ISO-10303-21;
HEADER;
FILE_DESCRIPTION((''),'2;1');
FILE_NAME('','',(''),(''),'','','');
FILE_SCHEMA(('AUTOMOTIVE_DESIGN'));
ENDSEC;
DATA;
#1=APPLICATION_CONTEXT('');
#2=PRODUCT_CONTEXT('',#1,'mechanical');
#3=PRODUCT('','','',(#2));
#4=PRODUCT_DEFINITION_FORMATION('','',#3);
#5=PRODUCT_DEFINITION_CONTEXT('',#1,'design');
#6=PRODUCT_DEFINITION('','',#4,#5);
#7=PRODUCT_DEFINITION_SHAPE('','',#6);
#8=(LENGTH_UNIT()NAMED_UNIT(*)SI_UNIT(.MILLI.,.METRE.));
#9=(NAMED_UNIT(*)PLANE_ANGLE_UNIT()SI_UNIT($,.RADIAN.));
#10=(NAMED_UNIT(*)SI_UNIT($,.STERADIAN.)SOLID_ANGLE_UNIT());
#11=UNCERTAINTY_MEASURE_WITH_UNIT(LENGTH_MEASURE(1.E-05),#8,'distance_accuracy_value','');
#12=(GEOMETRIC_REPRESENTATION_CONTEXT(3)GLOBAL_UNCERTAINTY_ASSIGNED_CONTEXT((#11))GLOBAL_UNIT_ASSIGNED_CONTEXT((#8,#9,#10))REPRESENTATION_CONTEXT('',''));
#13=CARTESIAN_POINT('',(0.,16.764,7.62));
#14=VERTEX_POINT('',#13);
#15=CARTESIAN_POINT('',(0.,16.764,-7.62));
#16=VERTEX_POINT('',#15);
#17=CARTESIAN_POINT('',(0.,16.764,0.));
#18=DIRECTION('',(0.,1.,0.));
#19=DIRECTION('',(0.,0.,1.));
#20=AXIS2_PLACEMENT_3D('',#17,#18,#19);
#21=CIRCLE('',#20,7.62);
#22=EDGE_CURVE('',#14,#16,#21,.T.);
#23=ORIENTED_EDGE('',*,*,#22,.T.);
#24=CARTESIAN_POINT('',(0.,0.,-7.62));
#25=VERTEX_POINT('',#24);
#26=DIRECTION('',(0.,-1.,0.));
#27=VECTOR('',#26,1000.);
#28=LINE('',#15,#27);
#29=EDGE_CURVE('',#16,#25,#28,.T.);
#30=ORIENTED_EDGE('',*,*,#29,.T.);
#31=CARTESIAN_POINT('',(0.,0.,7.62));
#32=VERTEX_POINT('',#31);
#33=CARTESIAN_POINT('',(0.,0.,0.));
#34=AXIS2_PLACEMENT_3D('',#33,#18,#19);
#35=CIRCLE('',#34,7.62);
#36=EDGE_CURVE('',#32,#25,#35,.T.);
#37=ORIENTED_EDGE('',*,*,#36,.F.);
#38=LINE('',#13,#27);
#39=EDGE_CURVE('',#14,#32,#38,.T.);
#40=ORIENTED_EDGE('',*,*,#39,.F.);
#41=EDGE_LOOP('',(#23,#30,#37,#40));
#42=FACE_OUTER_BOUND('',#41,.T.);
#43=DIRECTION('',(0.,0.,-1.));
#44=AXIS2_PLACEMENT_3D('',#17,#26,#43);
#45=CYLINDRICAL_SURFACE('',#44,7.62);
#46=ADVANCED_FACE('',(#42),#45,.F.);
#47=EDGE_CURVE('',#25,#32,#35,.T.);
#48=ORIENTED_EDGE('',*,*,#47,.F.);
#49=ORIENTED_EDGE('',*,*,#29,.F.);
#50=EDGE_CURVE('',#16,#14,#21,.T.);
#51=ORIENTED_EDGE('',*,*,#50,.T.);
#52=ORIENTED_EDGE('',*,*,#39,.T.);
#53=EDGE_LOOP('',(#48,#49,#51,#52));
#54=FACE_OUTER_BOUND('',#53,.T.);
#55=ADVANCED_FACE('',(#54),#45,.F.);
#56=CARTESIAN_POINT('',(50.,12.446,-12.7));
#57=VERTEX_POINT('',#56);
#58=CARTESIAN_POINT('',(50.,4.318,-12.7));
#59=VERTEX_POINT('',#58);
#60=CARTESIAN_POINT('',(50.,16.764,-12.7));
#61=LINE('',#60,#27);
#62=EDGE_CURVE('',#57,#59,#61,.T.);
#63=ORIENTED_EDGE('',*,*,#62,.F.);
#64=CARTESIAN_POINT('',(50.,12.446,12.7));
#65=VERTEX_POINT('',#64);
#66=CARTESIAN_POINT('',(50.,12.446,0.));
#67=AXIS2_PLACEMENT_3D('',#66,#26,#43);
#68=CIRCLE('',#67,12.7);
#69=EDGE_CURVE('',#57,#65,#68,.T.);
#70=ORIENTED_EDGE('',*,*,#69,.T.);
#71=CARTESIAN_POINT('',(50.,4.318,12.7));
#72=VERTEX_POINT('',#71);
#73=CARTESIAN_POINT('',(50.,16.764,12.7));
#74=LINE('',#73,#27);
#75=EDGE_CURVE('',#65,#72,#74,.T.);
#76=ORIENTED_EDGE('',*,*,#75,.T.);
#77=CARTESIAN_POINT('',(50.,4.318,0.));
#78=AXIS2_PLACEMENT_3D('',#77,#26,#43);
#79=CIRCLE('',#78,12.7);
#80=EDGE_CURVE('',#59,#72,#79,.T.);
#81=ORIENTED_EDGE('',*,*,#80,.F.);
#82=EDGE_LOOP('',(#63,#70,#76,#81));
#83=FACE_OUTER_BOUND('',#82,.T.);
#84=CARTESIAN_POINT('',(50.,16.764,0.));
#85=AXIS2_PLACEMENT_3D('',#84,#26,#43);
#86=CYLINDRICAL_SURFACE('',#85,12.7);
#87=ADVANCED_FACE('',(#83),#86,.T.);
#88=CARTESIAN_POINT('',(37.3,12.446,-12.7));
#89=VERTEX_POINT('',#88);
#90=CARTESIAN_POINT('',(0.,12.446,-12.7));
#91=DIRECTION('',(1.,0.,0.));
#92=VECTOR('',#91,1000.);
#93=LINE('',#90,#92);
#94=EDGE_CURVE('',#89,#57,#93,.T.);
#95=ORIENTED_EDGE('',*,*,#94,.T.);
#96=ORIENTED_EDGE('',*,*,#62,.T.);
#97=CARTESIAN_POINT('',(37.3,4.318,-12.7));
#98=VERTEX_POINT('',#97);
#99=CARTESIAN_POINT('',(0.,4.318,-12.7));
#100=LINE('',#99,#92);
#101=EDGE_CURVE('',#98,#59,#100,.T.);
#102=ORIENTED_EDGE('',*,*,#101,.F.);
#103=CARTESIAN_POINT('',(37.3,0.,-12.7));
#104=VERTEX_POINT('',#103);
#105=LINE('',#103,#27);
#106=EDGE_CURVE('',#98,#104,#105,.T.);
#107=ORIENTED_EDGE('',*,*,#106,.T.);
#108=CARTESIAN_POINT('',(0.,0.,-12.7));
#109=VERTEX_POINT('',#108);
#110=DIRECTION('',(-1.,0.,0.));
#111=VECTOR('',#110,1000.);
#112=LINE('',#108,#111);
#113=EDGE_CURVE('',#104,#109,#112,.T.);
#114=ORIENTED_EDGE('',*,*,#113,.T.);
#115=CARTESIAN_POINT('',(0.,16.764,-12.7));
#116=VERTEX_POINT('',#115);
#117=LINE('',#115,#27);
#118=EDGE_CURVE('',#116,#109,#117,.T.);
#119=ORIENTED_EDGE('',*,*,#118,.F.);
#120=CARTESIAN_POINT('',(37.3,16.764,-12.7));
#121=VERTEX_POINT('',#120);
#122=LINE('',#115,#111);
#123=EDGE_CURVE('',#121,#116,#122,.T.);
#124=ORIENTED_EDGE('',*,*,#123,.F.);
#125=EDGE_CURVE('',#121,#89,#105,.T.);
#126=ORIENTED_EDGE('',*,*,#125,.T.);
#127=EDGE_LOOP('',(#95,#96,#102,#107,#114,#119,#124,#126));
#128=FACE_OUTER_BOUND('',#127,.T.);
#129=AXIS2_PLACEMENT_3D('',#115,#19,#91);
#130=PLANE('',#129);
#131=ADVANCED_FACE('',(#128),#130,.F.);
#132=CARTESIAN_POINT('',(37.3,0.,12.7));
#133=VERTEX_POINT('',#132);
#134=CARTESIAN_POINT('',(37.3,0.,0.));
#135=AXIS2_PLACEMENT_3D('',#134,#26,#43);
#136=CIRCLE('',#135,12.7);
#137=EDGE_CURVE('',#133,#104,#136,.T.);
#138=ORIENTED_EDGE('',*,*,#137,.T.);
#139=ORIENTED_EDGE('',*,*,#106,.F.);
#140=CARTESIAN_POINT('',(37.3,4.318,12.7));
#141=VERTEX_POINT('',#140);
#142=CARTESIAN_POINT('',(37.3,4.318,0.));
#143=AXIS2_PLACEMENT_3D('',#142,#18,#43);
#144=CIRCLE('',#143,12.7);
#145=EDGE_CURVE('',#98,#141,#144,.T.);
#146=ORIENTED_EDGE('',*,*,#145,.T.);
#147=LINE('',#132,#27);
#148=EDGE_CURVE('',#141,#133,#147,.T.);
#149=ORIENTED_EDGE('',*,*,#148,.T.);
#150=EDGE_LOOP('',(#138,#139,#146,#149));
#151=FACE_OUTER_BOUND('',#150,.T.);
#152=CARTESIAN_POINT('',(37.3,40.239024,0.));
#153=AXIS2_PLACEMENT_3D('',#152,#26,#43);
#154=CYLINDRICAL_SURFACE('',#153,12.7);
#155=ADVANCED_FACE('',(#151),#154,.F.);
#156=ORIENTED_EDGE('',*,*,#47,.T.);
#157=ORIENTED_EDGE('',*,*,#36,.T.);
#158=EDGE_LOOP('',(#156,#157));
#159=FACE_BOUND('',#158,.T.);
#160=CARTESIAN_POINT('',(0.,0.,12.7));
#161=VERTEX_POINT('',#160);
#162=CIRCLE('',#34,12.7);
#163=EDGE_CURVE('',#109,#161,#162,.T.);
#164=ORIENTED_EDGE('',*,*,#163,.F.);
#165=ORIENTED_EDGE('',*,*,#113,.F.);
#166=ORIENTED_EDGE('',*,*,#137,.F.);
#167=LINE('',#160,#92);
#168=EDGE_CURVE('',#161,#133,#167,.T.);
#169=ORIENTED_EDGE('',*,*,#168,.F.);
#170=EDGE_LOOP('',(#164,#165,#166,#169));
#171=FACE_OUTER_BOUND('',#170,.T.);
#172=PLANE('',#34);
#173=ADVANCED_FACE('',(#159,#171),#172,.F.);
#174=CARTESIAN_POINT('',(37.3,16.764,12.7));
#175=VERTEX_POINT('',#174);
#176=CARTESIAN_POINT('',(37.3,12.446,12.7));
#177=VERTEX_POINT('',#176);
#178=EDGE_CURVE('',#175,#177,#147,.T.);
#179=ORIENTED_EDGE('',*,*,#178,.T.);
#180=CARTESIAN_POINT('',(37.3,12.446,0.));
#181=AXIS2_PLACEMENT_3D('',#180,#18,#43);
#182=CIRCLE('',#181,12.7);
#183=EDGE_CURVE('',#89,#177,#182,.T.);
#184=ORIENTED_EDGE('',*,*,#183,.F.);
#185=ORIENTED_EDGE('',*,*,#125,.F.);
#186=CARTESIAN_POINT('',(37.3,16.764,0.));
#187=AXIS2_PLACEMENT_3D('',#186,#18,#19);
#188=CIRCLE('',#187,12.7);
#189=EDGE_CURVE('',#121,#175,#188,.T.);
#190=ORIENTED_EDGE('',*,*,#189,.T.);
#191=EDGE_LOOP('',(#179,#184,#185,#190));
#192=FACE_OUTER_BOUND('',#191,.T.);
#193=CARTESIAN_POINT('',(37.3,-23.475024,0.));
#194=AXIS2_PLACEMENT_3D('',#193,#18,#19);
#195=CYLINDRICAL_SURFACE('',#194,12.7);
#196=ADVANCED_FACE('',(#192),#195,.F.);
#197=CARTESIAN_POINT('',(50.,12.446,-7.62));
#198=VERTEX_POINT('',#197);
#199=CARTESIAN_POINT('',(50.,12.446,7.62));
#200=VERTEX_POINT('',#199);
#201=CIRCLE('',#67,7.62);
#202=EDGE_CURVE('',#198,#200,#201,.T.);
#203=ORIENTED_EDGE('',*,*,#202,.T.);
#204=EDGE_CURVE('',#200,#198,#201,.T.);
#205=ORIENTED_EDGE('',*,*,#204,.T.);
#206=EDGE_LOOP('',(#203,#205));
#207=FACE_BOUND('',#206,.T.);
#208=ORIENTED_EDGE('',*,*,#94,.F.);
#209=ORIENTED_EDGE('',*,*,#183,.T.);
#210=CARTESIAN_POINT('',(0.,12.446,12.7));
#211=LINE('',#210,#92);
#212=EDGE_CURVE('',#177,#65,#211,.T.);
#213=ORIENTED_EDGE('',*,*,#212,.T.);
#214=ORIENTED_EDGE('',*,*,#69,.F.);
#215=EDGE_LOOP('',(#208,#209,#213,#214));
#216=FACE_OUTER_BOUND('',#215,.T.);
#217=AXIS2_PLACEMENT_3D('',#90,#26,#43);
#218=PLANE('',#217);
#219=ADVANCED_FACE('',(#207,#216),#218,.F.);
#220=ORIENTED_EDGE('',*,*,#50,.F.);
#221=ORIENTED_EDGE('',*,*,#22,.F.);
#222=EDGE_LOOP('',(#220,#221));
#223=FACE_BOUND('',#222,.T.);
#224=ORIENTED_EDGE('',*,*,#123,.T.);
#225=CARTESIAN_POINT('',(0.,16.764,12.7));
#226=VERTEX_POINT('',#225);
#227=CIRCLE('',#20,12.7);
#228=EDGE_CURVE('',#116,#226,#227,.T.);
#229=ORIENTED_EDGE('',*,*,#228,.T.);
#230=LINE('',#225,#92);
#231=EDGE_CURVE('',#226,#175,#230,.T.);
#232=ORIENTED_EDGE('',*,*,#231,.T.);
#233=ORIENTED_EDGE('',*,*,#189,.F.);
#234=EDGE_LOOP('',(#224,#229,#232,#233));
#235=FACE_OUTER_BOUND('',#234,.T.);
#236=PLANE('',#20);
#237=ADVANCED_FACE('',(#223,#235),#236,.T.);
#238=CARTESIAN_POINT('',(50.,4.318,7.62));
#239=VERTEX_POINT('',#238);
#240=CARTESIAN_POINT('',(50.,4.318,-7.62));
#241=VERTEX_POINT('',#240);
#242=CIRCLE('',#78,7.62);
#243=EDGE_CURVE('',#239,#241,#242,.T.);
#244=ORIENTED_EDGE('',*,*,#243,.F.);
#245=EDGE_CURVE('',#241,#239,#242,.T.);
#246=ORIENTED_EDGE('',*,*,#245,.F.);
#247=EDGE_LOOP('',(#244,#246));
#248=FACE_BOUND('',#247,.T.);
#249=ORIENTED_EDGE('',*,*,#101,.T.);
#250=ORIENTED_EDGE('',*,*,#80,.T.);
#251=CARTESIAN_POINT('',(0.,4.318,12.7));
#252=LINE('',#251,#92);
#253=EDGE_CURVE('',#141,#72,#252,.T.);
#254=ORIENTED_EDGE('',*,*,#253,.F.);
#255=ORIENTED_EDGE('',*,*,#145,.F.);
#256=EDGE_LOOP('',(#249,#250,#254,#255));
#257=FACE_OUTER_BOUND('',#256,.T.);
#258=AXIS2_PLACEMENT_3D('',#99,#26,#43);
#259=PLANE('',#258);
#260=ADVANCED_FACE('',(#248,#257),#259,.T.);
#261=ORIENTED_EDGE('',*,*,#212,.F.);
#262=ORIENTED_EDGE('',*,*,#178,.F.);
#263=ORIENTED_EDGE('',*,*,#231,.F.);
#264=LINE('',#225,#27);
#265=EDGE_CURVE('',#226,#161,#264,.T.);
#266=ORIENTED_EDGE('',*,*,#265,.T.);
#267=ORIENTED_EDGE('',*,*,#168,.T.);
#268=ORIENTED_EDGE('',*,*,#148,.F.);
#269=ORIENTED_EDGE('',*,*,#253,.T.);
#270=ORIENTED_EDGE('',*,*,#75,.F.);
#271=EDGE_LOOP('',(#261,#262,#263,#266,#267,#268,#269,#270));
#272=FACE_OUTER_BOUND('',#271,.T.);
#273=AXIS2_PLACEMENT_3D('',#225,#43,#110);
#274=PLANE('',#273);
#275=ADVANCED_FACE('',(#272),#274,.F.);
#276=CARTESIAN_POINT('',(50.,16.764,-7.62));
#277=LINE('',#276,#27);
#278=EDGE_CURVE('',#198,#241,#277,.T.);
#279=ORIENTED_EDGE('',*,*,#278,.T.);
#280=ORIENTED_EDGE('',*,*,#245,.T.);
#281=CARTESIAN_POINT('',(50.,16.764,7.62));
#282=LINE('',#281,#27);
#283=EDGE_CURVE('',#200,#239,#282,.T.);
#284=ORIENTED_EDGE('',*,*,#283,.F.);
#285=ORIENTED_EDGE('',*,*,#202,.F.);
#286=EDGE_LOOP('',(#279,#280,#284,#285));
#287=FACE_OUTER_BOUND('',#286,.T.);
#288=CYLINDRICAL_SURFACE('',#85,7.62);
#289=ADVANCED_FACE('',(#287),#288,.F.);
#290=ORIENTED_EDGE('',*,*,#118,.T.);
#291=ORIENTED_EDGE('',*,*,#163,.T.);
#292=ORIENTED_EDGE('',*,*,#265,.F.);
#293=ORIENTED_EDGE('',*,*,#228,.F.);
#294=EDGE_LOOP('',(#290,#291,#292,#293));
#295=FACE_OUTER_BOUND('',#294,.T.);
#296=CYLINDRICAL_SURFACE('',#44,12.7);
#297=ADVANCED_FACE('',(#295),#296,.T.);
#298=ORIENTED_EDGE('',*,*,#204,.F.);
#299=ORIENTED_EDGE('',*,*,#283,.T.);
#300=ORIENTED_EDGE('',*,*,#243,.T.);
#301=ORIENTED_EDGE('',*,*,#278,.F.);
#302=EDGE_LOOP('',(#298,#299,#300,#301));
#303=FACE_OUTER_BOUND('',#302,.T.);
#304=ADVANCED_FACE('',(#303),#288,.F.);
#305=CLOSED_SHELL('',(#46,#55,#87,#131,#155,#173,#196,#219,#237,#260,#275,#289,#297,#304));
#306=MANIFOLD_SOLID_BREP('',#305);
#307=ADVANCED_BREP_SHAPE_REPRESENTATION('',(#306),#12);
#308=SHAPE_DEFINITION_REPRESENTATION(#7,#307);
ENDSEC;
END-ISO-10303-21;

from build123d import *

# Parameters (mm, degrees)
SKETCH2_R           = 3.81
BOSS_EXTRUDE1_DEPTH = 8.382
SKETCH3_W           = 6.35
SKETCH3_H           = 2.159
CUT_EXTRUDE3_DEPTH  = 35.847818067
SKETCH4_R           = 6.35
CUT_EXTRUDE5_DEPTH  = 2.159
CUT_EXTRUDE6_START  = -2.159
SKETCH5_R           = 6.35
CUT_EXTRUDE6_DEPTH  = 2.159
SCALE1_SCALE        = 2


with BuildPart() as part:
    # Sketch2 → Boss-Extrude1 (new body)
    with BuildSketch(Plane(origin=(0, 0, 0), x_dir=(1, 0, 0), z_dir=(0, 1, 0))):
        with BuildLine():
            Line((0, 6.35), (25, 6.35))
            ThreePointArc((25, 6.35), (31.35, 0), (25, -6.35))
            Line((25, -6.35), (0, -6.35))
            ThreePointArc((0, -6.35), (-6.35, 0), (0, 6.35))
        make_face()
        with Locations(Location((0, 0, 0), (0, 0, 270))):
            Circle(SKETCH2_R, mode=Mode.SUBTRACT)
        with Locations(Location((25, 0, 0), (0, 0, 270))):
            Circle(SKETCH2_R, mode=Mode.SUBTRACT)
    extrude(amount=BOSS_EXTRUDE1_DEPTH)

    # Sketch3 → Cut-Extrude3 (cut, through all)
    with BuildSketch(Plane.XY.offset(6.35)):
        Polygon((52.142468872, 2.159), (25, 2.159), (25, 0), (54.039711746, 0), align=None)
        with Locations((21.825, 1.0795)):
            Rectangle(SKETCH3_W, SKETCH3_H)
        Polygon((49.831282098, 8.382), (25, 8.382), (25, 6.223), (51.556048347, 6.223), align=None)
        with Locations((21.825, 7.3025)):
            Rectangle(SKETCH3_W, SKETCH3_H)
    extrude(amount=-CUT_EXTRUDE3_DEPTH, mode=Mode.SUBTRACT)

    # Sketch4 → Cut-Extrude5 (cut)
    with BuildSketch(Plane.XZ):
        with Locations((18.65, 0)):
            Circle(SKETCH4_R)
    extrude(amount=-CUT_EXTRUDE5_DEPTH, mode=Mode.SUBTRACT)

    # Sketch5 → Cut-Extrude6 (cut)
    with BuildSketch(Plane(origin=(0, 8.382, 0), x_dir=(1, 0, 0), z_dir=(0, 1, 0)).offset(CUT_EXTRUDE6_START)):
        with Locations((18.65, 0)):
            Circle(SKETCH5_R)
    extrude(amount=CUT_EXTRUDE6_DEPTH, mode=Mode.SUBTRACT)


with BuildPart() as part_1:
    # Scale1: scaled about (0, 0, 0)
    add(part.part.scale(SCALE1_SCALE))


solid = part_1.part
